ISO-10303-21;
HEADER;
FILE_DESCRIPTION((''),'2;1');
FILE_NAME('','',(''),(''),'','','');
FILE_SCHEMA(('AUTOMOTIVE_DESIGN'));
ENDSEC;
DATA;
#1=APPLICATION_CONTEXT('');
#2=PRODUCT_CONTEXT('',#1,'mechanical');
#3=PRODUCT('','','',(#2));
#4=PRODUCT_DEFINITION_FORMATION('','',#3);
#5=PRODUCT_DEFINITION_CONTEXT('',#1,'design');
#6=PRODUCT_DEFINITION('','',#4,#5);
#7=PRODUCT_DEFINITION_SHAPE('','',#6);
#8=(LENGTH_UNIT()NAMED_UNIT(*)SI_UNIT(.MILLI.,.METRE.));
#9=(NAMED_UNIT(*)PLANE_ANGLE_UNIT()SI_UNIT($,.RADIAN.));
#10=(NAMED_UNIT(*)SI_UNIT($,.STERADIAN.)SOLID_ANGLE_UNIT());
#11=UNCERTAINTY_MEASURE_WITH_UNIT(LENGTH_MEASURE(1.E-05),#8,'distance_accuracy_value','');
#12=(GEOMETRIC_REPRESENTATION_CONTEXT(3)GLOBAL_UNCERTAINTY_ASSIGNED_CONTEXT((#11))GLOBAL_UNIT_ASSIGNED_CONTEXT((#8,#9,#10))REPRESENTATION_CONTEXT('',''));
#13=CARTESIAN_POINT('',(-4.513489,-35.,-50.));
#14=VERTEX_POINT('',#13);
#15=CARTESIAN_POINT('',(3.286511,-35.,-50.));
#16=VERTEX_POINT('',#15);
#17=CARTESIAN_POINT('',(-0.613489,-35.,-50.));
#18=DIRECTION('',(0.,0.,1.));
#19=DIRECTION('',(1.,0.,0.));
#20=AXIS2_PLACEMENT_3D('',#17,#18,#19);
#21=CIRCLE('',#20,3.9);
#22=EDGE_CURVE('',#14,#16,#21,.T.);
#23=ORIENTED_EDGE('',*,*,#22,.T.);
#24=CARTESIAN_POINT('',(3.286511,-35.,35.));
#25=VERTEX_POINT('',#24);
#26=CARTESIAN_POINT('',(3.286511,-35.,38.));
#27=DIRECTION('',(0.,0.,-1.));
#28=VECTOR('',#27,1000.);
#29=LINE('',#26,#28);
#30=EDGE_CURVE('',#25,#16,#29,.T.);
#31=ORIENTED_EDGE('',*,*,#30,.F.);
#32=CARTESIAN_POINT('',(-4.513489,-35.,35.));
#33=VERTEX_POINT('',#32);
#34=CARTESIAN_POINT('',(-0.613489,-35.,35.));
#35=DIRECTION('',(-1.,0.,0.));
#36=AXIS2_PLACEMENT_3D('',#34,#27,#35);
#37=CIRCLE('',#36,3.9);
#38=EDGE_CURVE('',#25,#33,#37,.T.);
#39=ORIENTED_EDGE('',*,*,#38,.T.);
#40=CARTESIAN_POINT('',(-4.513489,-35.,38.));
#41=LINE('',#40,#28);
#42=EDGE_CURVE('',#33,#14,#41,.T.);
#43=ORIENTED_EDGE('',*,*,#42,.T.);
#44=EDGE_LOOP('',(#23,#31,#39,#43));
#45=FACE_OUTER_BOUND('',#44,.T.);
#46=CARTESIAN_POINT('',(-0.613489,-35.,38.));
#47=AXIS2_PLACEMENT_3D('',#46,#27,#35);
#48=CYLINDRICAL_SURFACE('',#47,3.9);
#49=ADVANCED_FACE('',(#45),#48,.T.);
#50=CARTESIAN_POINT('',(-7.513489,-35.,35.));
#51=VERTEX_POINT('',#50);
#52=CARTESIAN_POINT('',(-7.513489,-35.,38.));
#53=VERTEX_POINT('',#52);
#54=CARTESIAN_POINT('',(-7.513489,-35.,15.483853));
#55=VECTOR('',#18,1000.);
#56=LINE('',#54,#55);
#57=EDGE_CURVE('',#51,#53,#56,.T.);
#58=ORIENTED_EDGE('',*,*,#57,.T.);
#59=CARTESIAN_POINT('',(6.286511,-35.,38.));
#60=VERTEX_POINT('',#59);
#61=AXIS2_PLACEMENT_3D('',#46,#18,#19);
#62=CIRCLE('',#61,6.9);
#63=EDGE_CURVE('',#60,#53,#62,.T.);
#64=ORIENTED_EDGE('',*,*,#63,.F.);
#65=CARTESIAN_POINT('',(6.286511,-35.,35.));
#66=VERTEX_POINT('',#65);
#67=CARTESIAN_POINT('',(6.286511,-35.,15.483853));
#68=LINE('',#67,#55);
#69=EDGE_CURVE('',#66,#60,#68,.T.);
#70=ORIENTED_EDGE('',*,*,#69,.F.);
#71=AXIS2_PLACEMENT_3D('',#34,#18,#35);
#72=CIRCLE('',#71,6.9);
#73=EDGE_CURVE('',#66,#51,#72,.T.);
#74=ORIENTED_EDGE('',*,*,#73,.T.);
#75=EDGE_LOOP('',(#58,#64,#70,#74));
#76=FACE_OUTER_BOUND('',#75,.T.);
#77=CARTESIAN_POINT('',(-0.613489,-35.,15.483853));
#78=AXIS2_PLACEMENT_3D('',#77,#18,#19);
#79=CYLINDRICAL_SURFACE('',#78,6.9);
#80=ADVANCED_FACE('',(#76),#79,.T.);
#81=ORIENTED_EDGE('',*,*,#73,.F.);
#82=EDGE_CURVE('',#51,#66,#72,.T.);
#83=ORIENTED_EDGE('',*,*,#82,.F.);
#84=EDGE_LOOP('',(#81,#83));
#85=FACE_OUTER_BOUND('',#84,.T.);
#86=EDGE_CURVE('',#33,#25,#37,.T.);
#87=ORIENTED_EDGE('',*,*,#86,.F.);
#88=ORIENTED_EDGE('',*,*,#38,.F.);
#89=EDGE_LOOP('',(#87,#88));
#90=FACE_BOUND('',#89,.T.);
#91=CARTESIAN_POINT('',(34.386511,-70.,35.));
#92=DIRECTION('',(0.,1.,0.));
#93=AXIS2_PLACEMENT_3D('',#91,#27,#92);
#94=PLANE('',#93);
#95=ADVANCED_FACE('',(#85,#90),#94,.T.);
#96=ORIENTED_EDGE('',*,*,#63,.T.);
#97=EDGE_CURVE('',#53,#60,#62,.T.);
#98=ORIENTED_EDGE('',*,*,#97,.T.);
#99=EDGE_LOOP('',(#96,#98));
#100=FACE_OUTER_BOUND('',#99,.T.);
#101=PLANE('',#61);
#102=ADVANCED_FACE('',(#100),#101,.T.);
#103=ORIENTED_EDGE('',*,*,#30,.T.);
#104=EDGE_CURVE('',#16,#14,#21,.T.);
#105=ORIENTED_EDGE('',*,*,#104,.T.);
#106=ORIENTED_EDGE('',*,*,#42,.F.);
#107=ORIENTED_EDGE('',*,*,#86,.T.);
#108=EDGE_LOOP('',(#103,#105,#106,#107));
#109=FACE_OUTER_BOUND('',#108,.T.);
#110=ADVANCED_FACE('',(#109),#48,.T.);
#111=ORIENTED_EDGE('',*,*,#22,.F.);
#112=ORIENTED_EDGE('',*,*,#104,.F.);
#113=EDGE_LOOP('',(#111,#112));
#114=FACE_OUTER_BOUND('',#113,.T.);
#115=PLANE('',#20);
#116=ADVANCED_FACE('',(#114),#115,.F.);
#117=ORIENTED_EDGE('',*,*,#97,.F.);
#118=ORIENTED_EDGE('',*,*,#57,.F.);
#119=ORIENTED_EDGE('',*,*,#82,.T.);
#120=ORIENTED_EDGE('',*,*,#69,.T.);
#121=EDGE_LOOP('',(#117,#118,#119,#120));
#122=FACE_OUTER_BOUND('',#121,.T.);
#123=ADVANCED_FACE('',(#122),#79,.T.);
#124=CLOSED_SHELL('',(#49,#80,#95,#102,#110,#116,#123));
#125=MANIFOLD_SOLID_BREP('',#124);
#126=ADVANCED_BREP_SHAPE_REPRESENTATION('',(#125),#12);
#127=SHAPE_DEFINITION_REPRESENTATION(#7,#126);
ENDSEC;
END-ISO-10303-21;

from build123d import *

# Parameters (mm, degrees)
BOSS_EXTRUDE1_DEPTH      = 38
BOSS_EXTRUDE1_DEPTH_BACK = 50
SKETCH1_R                = 3.9
SKETCH2_R                = 6.9
BOSS_EXTRUDE2_DEPTH      = 3


with BuildPart() as part:
    # Sketch1 → Boss-Extrude1 (new, two sides: drawn at the far end of the back side and taken through both)
    with BuildSketch(Plane.XY.offset(-BOSS_EXTRUDE1_DEPTH_BACK)):
        with Locations((-0.613489308, -35)):
            Circle(SKETCH1_R)
    extrude(amount=BOSS_EXTRUDE1_DEPTH + BOSS_EXTRUDE1_DEPTH_BACK)

    # Sketch2 → Boss-Extrude2 (add)
    with BuildSketch(Plane.XY.offset(38)):
        with Locations((-0.613489308, -35)):
            Circle(SKETCH2_R)
    extrude(amount=-BOSS_EXTRUDE2_DEPTH)


solid = part.part
